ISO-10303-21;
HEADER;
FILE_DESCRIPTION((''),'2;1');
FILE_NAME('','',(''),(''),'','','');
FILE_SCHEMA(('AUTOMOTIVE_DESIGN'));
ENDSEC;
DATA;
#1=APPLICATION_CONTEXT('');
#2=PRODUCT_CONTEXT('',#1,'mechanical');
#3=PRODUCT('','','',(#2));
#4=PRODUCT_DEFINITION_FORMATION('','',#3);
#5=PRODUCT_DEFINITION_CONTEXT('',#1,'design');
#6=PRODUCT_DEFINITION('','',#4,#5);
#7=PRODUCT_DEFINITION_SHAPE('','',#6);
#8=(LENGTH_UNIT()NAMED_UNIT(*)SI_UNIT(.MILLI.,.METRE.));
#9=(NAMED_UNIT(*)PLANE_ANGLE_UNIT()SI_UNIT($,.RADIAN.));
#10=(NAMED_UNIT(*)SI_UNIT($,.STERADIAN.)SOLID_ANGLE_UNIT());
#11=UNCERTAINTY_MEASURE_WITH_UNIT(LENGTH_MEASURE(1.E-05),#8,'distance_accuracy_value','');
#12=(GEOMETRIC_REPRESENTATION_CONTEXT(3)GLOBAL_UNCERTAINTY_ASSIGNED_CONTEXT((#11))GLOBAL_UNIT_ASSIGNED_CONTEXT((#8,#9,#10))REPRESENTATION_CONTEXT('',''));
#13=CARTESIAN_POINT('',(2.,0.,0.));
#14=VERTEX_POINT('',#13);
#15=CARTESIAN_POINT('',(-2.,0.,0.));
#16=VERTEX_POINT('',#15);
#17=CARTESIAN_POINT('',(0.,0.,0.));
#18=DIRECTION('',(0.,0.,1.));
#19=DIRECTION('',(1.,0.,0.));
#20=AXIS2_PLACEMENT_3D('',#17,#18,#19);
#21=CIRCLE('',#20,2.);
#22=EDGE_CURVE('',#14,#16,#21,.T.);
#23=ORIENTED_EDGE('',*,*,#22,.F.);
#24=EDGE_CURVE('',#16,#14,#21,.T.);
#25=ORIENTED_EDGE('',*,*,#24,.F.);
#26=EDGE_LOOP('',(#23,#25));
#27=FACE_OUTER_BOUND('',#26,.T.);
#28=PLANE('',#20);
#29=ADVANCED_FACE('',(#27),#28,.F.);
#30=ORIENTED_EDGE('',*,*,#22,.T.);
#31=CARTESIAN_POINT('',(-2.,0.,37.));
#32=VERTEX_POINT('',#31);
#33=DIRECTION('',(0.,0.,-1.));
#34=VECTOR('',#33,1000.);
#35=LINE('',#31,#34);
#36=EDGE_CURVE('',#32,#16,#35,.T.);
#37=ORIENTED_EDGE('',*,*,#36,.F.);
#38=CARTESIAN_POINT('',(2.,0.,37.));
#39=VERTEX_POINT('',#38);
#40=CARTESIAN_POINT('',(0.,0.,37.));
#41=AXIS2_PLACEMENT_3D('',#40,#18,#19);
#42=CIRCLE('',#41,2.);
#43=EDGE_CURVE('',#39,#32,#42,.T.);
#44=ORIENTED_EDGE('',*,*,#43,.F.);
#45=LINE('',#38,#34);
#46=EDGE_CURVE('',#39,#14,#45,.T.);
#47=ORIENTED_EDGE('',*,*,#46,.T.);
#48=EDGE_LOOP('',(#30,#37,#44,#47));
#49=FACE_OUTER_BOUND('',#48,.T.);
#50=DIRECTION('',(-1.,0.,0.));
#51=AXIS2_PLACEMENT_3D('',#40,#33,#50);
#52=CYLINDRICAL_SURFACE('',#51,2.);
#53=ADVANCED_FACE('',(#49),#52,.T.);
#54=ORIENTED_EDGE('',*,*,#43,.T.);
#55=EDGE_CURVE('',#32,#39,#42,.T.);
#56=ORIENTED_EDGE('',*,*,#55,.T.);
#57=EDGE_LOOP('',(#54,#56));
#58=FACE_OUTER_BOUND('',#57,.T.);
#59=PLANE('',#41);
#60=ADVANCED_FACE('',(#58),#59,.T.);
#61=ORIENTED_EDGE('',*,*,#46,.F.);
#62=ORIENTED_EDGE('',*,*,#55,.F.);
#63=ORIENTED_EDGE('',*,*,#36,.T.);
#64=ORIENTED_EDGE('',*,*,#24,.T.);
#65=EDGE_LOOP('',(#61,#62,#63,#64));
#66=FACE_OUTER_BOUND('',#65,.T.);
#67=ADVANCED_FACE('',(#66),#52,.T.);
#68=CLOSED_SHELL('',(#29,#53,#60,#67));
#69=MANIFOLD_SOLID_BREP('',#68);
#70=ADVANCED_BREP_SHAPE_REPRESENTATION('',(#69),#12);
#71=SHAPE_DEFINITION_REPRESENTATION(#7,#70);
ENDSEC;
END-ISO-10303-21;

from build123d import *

# Parameters (mm, degrees)
SKETCH_1_R      = 2
EXTRUDE_1_DEPTH = 37


with BuildPart() as part:
    # 草图1 → 凸台-拉伸1 (new body)
    with BuildSketch(Plane.XY):
        Circle(SKETCH_1_R)
    extrude(amount=EXTRUDE_1_DEPTH)


solid = part.part
